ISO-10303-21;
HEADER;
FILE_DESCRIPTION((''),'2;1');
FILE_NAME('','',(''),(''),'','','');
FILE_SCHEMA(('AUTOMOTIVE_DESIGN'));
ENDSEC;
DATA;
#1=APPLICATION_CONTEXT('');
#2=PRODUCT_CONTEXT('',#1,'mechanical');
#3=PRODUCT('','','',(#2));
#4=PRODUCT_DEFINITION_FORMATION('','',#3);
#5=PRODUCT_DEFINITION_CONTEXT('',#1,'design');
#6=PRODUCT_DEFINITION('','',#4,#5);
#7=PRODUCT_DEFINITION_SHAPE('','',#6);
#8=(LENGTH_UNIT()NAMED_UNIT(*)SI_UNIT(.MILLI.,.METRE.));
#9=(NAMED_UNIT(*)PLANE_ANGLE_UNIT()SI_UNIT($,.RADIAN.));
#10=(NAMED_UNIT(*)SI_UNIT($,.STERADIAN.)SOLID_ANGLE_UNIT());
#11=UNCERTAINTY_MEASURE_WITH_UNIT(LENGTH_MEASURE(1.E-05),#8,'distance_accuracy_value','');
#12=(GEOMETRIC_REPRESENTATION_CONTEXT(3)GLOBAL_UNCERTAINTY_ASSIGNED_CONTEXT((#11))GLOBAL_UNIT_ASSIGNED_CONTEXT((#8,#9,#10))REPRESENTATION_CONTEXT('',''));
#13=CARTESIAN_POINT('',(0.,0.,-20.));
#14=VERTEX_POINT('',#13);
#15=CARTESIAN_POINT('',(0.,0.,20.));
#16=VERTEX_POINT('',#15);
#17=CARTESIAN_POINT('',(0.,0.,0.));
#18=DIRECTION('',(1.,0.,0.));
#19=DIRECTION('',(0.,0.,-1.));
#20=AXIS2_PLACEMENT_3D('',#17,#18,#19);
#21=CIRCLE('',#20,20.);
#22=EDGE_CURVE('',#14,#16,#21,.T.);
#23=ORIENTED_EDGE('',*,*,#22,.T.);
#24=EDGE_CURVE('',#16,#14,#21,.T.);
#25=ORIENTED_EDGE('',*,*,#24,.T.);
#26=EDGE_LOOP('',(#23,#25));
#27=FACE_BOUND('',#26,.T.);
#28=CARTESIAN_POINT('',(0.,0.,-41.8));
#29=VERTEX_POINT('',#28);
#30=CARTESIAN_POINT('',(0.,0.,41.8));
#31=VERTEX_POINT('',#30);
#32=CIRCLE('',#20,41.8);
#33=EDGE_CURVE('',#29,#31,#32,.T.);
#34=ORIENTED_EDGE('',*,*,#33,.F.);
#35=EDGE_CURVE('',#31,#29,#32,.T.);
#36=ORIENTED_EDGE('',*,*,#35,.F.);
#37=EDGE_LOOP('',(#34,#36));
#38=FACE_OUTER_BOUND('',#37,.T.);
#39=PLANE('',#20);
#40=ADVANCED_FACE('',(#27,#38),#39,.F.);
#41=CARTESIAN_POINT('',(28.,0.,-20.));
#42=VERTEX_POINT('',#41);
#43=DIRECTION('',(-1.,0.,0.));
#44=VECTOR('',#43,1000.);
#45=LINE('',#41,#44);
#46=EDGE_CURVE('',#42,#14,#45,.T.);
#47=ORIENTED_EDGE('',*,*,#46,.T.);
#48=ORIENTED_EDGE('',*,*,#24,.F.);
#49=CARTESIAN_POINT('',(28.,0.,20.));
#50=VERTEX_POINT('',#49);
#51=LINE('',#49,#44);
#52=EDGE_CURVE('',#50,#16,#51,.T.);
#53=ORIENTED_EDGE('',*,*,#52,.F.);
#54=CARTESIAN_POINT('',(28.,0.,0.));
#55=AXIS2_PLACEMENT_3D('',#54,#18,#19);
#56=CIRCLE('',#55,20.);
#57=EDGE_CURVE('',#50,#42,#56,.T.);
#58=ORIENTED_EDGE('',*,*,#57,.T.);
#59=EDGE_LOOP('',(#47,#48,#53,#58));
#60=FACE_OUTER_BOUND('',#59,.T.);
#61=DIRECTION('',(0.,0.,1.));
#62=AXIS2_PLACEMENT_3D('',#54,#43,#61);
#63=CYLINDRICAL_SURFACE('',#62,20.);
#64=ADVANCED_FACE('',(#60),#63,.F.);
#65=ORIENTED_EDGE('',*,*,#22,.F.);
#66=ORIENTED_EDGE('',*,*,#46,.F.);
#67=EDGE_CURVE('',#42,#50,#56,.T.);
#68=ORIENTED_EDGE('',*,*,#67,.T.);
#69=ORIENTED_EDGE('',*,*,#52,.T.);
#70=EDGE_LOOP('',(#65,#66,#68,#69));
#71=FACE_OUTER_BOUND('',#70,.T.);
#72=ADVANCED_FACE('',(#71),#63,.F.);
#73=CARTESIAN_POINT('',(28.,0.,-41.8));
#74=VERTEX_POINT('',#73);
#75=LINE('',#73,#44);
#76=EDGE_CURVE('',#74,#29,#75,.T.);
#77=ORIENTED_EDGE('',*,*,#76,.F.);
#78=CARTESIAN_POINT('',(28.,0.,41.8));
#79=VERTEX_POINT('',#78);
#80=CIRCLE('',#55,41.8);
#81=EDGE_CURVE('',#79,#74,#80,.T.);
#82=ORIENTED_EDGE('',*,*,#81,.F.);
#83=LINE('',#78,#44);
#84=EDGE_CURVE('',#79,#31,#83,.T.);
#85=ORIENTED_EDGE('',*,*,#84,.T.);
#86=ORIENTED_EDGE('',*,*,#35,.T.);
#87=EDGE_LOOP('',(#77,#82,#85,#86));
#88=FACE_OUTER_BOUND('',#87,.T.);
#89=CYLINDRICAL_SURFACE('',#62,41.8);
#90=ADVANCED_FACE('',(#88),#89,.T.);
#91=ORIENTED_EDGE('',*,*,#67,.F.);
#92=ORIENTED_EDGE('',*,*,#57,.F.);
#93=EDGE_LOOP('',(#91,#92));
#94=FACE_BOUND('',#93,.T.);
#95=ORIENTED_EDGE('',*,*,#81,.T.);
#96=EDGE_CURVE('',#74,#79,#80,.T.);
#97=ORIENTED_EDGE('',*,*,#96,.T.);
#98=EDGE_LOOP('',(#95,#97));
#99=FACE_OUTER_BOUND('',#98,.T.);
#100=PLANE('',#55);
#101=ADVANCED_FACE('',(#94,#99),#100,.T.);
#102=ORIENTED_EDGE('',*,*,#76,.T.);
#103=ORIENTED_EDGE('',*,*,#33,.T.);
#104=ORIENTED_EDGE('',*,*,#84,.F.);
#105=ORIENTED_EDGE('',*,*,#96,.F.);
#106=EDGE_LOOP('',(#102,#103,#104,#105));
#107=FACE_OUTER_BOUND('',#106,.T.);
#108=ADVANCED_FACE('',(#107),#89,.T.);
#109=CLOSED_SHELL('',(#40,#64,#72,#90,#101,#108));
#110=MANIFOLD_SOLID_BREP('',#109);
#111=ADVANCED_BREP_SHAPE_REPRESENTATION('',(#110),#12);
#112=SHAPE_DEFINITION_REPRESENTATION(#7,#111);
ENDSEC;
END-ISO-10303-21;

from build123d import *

# Parameters (mm, degrees)
SKETCH_1_R      = 41.8
SKETCH_1_R_2    = 20
EXTRUDE_1_DEPTH = 28


with BuildPart() as part:
    # 草图1 → 凸台-拉伸1 (new body)
    with BuildSketch(Plane(origin=(0, 0, 0), x_dir=(0, 0, -1), z_dir=(1, 0, 0))):
        Circle(SKETCH_1_R)
        Circle(SKETCH_1_R_2, mode=Mode.SUBTRACT)
    extrude(amount=EXTRUDE_1_DEPTH)


solid = part.part
